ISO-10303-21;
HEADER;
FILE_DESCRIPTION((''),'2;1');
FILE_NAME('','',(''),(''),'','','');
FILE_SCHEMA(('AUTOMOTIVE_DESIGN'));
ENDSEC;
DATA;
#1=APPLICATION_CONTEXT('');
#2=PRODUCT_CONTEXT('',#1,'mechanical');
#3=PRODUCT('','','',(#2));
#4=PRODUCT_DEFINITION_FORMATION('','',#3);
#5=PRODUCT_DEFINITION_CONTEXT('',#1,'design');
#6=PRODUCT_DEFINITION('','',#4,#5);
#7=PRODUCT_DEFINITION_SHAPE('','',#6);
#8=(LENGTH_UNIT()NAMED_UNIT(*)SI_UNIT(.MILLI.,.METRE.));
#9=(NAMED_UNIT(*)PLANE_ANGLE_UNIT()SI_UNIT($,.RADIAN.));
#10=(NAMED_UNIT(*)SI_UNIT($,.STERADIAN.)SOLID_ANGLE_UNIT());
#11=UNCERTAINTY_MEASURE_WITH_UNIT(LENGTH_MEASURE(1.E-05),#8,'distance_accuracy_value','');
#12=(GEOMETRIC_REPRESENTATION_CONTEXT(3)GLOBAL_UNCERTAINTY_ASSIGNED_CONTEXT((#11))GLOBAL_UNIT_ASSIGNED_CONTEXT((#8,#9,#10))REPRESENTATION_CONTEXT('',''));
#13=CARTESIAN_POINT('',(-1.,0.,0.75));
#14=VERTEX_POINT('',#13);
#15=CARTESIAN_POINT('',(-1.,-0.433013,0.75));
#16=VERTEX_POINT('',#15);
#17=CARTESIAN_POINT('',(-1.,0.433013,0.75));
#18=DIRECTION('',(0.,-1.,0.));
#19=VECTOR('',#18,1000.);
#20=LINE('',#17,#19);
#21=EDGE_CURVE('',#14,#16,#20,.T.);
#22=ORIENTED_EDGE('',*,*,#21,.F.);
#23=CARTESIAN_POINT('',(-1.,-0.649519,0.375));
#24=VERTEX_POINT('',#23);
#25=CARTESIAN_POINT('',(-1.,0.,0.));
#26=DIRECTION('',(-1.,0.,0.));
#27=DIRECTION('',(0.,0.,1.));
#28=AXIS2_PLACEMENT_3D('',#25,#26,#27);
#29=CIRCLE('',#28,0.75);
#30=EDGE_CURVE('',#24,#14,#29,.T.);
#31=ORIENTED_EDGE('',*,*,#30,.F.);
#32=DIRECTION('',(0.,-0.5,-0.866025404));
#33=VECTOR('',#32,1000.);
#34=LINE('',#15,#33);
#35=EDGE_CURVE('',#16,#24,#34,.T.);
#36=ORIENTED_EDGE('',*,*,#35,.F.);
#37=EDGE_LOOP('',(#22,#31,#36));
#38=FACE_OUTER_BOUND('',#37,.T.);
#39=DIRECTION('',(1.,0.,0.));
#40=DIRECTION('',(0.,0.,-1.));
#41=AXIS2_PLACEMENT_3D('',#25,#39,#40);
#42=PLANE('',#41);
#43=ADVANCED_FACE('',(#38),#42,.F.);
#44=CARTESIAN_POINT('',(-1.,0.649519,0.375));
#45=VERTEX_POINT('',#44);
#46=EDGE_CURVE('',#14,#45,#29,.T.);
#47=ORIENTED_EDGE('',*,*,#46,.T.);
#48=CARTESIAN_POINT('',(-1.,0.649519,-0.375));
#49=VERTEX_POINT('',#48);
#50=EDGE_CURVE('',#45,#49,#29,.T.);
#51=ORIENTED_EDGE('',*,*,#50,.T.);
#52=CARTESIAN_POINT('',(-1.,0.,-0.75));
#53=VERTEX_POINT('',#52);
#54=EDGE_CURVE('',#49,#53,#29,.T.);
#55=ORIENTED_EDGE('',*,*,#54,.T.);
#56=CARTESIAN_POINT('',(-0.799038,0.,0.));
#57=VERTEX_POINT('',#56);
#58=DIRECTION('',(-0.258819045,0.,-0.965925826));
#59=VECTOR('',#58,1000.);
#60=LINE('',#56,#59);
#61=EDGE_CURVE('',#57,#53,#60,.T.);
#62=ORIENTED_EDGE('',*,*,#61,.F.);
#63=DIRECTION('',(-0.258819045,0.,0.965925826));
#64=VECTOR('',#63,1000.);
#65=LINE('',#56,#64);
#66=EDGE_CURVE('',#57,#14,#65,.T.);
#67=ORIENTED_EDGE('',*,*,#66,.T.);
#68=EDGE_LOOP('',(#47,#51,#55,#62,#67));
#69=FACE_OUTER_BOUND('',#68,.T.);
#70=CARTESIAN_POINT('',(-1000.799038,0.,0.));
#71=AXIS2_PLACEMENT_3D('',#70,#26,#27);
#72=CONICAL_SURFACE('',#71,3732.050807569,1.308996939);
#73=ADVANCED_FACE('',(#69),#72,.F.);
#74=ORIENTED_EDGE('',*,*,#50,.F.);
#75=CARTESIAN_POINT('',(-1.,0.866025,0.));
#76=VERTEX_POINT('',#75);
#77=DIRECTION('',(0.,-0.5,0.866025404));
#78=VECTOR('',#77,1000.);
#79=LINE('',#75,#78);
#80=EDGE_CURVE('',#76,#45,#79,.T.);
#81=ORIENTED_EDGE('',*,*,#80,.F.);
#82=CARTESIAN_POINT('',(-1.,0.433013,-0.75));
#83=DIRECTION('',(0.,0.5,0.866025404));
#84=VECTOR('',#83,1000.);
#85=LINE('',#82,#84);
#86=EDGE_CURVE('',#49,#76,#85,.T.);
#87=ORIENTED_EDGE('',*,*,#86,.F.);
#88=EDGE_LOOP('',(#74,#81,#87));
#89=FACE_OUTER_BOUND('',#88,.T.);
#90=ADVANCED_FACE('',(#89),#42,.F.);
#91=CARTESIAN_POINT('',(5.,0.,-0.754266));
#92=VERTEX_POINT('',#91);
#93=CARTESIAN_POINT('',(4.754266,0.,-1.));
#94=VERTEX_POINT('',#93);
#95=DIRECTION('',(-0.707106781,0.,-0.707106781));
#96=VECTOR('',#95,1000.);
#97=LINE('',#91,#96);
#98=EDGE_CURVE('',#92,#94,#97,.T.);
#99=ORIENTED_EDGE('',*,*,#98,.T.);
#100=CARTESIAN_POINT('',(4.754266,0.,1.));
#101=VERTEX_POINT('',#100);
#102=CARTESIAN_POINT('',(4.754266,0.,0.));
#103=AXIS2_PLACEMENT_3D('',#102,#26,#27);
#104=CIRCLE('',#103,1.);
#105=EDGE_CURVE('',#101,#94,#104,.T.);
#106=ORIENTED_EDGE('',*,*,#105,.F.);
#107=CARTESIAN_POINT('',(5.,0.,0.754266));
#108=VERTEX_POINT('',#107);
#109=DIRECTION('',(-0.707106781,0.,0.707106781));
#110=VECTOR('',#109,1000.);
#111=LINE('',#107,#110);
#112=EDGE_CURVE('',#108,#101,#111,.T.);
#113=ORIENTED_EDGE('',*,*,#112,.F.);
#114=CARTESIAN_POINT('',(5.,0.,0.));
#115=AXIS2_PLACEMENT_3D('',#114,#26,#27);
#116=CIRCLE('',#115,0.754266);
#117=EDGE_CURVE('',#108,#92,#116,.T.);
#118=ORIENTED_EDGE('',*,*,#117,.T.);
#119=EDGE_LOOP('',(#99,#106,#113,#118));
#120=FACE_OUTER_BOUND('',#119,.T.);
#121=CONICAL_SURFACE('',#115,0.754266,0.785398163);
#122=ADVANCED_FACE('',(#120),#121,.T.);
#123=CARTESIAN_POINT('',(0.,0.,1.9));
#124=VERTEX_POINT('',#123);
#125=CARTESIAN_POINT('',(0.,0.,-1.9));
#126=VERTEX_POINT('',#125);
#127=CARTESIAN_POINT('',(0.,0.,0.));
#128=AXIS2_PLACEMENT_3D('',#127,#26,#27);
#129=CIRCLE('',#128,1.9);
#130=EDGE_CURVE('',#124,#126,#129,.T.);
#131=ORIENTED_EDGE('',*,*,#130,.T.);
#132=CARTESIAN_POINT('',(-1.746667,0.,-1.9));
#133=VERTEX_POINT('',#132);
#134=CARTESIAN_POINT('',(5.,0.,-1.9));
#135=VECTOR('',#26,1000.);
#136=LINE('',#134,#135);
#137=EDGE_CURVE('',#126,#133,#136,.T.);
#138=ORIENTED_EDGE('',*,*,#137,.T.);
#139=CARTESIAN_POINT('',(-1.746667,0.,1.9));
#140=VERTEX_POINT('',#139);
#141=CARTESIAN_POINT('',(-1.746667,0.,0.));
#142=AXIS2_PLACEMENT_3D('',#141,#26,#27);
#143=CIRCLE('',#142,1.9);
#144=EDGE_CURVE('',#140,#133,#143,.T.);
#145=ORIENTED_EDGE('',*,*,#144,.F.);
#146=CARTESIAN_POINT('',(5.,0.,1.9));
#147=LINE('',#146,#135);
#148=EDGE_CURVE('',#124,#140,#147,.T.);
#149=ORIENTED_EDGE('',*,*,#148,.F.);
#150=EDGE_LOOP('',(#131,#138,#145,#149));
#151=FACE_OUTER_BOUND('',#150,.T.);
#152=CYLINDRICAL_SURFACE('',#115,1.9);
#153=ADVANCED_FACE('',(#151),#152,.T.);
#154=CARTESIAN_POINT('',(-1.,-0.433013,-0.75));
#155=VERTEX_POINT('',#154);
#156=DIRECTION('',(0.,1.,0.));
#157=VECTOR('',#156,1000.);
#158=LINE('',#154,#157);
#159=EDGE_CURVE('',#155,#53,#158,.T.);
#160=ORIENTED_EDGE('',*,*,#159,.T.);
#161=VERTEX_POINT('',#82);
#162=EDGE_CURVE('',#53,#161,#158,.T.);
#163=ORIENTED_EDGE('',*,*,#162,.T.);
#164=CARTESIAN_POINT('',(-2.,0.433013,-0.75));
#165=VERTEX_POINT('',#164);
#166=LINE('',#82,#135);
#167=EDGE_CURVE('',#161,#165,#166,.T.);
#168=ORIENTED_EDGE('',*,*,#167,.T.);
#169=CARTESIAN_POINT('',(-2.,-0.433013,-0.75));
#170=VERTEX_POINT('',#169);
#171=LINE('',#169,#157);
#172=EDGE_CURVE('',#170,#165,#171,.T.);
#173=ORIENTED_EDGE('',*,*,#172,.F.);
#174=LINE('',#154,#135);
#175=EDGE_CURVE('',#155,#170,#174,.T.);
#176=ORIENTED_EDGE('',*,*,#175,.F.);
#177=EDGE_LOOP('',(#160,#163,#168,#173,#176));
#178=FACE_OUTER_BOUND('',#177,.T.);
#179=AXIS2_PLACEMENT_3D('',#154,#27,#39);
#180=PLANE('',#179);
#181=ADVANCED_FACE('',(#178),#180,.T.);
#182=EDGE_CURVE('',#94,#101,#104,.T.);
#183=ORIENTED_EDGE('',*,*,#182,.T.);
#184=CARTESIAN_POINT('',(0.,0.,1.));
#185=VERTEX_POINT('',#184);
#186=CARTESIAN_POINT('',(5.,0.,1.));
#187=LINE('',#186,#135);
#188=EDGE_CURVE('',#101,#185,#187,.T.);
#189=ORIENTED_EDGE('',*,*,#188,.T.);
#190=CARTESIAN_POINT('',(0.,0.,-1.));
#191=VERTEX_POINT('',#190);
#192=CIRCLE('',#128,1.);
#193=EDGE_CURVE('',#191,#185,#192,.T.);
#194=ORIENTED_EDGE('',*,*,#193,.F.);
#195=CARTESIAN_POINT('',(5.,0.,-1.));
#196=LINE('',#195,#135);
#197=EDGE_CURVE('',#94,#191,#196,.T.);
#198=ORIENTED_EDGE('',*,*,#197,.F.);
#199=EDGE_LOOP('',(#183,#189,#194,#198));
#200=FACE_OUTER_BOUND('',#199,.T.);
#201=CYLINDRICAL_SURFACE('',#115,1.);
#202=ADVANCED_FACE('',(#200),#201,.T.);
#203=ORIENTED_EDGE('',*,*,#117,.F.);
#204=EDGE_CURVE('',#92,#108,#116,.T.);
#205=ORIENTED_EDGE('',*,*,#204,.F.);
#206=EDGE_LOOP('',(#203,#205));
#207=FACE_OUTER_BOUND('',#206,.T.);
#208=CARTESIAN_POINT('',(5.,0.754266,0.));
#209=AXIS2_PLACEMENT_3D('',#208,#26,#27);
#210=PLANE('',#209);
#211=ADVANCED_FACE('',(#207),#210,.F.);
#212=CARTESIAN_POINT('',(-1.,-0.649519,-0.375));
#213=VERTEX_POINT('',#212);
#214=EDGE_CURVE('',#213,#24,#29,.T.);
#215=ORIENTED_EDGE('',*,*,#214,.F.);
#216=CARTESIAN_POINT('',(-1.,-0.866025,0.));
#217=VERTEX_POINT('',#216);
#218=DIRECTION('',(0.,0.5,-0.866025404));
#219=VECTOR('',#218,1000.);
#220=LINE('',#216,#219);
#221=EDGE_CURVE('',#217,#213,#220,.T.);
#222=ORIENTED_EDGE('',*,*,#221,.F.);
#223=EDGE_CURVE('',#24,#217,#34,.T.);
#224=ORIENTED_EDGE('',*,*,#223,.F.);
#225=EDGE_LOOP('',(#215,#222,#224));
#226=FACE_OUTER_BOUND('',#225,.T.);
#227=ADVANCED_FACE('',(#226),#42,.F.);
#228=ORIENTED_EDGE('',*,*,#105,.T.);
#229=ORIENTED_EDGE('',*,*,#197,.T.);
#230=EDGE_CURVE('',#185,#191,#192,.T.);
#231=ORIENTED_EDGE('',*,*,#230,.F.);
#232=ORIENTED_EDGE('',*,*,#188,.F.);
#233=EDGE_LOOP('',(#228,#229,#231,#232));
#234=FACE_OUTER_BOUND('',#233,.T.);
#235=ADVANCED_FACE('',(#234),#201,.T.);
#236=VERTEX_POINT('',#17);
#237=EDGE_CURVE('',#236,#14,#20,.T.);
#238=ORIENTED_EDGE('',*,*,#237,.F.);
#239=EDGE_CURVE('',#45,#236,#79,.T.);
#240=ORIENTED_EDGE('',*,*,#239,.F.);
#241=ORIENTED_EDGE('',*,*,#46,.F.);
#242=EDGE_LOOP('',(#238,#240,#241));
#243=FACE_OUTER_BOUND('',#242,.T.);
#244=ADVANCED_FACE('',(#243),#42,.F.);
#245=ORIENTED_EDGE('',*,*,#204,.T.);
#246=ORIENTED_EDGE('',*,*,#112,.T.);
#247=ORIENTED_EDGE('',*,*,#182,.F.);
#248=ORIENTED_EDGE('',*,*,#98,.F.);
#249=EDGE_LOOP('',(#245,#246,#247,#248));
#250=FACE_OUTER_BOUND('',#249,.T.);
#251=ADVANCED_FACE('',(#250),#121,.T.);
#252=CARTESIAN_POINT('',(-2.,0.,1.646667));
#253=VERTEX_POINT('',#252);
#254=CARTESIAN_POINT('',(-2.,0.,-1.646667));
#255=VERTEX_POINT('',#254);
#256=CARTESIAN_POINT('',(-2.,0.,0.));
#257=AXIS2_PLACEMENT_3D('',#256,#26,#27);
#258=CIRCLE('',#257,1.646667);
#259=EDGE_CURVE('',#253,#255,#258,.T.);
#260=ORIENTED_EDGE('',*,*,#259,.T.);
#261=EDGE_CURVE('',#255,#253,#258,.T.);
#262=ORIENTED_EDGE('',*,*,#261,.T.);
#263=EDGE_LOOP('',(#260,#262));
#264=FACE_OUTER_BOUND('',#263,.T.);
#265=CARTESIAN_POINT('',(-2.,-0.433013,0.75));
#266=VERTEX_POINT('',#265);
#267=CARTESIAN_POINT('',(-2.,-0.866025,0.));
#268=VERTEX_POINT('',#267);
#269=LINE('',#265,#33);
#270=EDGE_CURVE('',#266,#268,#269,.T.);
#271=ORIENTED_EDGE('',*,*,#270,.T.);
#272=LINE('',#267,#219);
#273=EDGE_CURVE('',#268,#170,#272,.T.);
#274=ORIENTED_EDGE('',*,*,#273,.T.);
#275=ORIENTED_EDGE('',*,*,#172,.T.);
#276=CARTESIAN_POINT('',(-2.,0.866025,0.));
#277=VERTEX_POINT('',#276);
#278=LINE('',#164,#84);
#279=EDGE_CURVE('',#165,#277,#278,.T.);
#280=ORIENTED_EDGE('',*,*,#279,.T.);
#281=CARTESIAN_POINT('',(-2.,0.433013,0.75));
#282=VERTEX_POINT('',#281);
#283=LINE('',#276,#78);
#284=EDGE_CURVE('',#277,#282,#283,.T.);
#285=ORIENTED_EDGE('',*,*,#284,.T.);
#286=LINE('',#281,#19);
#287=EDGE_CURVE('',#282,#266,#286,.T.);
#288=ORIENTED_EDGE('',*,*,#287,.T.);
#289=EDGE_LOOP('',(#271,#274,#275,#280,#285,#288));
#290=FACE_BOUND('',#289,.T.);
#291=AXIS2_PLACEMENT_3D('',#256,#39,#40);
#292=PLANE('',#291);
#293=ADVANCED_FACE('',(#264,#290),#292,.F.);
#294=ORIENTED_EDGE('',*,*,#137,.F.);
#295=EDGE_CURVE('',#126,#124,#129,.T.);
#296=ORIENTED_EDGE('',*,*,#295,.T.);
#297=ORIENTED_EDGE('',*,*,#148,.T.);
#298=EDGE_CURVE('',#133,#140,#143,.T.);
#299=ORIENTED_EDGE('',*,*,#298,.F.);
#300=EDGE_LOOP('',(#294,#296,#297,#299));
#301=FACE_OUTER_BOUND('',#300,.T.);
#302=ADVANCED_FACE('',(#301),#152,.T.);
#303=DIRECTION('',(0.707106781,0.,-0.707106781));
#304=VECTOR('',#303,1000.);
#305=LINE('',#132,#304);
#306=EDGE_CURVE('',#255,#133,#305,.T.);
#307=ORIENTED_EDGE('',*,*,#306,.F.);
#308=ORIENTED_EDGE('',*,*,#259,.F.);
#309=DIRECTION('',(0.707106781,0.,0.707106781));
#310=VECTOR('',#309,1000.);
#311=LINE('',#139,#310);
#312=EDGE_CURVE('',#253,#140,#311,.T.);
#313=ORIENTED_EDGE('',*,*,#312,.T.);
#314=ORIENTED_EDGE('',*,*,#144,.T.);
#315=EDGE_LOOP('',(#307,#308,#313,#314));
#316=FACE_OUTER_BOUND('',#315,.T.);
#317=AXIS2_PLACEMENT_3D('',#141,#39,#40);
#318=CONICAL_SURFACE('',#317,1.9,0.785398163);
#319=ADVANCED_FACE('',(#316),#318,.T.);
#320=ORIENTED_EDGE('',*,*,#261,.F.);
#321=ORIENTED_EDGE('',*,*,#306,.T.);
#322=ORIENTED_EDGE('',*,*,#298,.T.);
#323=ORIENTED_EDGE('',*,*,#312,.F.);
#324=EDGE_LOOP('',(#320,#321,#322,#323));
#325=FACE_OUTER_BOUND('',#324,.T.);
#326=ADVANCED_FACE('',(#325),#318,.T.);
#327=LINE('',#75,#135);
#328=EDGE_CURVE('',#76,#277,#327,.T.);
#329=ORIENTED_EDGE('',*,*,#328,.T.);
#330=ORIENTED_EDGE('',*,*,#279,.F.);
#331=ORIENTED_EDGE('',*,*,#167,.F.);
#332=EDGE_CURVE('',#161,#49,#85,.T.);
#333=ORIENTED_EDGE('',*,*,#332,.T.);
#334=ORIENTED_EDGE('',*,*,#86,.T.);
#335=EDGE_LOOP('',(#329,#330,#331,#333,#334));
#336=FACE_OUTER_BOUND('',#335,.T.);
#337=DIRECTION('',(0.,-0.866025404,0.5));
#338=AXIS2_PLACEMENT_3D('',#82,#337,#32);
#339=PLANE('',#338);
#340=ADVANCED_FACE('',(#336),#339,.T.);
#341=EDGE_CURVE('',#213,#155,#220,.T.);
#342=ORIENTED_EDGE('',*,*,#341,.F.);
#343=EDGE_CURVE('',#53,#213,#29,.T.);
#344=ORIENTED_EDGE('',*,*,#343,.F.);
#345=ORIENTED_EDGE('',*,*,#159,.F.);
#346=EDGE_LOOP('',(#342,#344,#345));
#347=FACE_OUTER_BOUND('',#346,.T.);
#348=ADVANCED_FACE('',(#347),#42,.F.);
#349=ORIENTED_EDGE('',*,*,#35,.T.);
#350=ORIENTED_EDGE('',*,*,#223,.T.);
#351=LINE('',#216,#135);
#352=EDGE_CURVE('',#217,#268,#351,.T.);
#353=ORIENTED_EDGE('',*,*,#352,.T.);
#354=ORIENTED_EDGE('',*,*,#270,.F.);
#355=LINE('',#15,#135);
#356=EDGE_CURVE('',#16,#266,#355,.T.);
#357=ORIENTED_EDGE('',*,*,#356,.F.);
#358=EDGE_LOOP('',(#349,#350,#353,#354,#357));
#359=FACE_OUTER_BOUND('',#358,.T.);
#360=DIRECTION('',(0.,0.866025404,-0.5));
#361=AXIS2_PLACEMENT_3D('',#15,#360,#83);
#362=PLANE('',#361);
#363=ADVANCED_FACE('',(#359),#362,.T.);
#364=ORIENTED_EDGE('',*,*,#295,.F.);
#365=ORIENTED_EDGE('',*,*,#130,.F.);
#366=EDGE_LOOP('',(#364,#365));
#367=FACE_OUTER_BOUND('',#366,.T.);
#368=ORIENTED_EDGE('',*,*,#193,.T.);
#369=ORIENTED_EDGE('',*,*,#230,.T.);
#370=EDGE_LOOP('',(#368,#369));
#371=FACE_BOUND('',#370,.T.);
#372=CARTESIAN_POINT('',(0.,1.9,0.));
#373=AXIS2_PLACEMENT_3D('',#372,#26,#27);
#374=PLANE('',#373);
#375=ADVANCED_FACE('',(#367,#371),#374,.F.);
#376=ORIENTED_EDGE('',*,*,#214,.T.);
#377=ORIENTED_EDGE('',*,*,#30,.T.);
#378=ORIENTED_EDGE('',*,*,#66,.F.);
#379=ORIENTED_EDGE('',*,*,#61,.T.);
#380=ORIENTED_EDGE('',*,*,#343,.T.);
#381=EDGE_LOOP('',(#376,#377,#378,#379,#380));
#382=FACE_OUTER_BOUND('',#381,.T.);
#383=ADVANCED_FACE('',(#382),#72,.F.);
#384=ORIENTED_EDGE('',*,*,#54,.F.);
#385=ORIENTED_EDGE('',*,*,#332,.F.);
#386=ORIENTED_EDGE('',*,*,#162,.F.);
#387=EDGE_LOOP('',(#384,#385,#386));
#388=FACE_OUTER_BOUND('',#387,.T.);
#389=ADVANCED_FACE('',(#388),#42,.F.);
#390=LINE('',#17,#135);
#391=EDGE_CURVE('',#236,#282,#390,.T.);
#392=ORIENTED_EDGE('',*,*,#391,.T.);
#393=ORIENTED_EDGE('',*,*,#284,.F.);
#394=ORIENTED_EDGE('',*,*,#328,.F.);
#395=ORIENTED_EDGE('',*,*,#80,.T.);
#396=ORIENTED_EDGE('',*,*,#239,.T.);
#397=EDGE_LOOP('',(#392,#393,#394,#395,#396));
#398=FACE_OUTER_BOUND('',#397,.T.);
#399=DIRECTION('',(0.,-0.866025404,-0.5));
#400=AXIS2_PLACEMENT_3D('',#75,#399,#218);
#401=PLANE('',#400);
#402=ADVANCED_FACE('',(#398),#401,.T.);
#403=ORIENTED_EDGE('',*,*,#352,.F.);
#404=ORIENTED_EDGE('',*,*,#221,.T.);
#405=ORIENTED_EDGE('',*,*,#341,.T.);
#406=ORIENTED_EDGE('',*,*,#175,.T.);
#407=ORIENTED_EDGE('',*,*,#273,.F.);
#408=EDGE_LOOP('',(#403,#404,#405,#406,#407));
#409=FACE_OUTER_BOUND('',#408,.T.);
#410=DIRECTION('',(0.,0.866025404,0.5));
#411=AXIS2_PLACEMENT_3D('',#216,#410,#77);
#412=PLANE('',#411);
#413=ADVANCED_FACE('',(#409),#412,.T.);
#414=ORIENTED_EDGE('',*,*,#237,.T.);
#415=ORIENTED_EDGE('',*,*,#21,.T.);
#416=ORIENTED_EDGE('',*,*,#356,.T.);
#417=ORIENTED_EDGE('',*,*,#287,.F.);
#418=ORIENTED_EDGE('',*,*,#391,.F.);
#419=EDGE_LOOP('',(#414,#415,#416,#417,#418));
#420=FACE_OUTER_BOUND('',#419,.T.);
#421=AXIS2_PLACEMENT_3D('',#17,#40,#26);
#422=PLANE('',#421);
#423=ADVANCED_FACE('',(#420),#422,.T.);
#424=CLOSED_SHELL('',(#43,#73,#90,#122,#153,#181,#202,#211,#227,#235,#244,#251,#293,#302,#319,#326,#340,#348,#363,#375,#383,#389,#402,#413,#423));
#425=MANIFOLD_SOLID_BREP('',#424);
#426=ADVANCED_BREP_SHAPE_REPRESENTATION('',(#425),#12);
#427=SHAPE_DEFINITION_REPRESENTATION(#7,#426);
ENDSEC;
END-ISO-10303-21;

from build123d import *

# Parameters (mm, degrees)
CUT_EXTRUDE1_DEPTH = 1


with BuildPart() as part:
    # Sketch1 → Revolve1 (revolve)
    with BuildSketch(Plane.XY, mode=Mode.PRIVATE) as revolve1_sk:
        Polygon((-2, 0), (-2, 1.646666667), (-1.746666667, 1.9), (0, 1.9), (0, 1), (4.754266, 1), (5, 0.754266), (5, 0), align=None)
    revolve(revolve1_sk.sketch.rotate(Axis((5, 0, 0), (-1, 0, 0)), 270), axis=Axis((5, 0, 0), (-1, 0, 0)))

    # Sketch2 → Cut-Revolve1 (revolve, cut)
    with BuildSketch(Plane.XY, mode=Mode.PRIVATE) as cut_revolve1_sk:
        Polygon((-2, 0), (-2, 0.75), (-1, 0.75), (-0.799038106, 0), align=None)
    revolve(cut_revolve1_sk.sketch.rotate(Axis((-0.799038106, 0, 0), (-1, 0, 0)), 270), axis=Axis((-0.799038106, 0, 0), (-1, 0, 0)), mode=Mode.SUBTRACT)

    # Sketch3 → Cut-Extrude1 (cut)
    with BuildSketch(Plane(origin=(-2, 0, 0), x_dir=(0, 0, -1), z_dir=(1, 0, 0))):
        Polygon((-0.75, 0.433012702), (-0.75, -0.433012702), (0, -0.866025404), (0.75, -0.433012702), (0.75, 0.433012702), (0, 0.866025404), align=None)
    extrude(amount=CUT_EXTRUDE1_DEPTH, mode=Mode.SUBTRACT)


solid = part.part
